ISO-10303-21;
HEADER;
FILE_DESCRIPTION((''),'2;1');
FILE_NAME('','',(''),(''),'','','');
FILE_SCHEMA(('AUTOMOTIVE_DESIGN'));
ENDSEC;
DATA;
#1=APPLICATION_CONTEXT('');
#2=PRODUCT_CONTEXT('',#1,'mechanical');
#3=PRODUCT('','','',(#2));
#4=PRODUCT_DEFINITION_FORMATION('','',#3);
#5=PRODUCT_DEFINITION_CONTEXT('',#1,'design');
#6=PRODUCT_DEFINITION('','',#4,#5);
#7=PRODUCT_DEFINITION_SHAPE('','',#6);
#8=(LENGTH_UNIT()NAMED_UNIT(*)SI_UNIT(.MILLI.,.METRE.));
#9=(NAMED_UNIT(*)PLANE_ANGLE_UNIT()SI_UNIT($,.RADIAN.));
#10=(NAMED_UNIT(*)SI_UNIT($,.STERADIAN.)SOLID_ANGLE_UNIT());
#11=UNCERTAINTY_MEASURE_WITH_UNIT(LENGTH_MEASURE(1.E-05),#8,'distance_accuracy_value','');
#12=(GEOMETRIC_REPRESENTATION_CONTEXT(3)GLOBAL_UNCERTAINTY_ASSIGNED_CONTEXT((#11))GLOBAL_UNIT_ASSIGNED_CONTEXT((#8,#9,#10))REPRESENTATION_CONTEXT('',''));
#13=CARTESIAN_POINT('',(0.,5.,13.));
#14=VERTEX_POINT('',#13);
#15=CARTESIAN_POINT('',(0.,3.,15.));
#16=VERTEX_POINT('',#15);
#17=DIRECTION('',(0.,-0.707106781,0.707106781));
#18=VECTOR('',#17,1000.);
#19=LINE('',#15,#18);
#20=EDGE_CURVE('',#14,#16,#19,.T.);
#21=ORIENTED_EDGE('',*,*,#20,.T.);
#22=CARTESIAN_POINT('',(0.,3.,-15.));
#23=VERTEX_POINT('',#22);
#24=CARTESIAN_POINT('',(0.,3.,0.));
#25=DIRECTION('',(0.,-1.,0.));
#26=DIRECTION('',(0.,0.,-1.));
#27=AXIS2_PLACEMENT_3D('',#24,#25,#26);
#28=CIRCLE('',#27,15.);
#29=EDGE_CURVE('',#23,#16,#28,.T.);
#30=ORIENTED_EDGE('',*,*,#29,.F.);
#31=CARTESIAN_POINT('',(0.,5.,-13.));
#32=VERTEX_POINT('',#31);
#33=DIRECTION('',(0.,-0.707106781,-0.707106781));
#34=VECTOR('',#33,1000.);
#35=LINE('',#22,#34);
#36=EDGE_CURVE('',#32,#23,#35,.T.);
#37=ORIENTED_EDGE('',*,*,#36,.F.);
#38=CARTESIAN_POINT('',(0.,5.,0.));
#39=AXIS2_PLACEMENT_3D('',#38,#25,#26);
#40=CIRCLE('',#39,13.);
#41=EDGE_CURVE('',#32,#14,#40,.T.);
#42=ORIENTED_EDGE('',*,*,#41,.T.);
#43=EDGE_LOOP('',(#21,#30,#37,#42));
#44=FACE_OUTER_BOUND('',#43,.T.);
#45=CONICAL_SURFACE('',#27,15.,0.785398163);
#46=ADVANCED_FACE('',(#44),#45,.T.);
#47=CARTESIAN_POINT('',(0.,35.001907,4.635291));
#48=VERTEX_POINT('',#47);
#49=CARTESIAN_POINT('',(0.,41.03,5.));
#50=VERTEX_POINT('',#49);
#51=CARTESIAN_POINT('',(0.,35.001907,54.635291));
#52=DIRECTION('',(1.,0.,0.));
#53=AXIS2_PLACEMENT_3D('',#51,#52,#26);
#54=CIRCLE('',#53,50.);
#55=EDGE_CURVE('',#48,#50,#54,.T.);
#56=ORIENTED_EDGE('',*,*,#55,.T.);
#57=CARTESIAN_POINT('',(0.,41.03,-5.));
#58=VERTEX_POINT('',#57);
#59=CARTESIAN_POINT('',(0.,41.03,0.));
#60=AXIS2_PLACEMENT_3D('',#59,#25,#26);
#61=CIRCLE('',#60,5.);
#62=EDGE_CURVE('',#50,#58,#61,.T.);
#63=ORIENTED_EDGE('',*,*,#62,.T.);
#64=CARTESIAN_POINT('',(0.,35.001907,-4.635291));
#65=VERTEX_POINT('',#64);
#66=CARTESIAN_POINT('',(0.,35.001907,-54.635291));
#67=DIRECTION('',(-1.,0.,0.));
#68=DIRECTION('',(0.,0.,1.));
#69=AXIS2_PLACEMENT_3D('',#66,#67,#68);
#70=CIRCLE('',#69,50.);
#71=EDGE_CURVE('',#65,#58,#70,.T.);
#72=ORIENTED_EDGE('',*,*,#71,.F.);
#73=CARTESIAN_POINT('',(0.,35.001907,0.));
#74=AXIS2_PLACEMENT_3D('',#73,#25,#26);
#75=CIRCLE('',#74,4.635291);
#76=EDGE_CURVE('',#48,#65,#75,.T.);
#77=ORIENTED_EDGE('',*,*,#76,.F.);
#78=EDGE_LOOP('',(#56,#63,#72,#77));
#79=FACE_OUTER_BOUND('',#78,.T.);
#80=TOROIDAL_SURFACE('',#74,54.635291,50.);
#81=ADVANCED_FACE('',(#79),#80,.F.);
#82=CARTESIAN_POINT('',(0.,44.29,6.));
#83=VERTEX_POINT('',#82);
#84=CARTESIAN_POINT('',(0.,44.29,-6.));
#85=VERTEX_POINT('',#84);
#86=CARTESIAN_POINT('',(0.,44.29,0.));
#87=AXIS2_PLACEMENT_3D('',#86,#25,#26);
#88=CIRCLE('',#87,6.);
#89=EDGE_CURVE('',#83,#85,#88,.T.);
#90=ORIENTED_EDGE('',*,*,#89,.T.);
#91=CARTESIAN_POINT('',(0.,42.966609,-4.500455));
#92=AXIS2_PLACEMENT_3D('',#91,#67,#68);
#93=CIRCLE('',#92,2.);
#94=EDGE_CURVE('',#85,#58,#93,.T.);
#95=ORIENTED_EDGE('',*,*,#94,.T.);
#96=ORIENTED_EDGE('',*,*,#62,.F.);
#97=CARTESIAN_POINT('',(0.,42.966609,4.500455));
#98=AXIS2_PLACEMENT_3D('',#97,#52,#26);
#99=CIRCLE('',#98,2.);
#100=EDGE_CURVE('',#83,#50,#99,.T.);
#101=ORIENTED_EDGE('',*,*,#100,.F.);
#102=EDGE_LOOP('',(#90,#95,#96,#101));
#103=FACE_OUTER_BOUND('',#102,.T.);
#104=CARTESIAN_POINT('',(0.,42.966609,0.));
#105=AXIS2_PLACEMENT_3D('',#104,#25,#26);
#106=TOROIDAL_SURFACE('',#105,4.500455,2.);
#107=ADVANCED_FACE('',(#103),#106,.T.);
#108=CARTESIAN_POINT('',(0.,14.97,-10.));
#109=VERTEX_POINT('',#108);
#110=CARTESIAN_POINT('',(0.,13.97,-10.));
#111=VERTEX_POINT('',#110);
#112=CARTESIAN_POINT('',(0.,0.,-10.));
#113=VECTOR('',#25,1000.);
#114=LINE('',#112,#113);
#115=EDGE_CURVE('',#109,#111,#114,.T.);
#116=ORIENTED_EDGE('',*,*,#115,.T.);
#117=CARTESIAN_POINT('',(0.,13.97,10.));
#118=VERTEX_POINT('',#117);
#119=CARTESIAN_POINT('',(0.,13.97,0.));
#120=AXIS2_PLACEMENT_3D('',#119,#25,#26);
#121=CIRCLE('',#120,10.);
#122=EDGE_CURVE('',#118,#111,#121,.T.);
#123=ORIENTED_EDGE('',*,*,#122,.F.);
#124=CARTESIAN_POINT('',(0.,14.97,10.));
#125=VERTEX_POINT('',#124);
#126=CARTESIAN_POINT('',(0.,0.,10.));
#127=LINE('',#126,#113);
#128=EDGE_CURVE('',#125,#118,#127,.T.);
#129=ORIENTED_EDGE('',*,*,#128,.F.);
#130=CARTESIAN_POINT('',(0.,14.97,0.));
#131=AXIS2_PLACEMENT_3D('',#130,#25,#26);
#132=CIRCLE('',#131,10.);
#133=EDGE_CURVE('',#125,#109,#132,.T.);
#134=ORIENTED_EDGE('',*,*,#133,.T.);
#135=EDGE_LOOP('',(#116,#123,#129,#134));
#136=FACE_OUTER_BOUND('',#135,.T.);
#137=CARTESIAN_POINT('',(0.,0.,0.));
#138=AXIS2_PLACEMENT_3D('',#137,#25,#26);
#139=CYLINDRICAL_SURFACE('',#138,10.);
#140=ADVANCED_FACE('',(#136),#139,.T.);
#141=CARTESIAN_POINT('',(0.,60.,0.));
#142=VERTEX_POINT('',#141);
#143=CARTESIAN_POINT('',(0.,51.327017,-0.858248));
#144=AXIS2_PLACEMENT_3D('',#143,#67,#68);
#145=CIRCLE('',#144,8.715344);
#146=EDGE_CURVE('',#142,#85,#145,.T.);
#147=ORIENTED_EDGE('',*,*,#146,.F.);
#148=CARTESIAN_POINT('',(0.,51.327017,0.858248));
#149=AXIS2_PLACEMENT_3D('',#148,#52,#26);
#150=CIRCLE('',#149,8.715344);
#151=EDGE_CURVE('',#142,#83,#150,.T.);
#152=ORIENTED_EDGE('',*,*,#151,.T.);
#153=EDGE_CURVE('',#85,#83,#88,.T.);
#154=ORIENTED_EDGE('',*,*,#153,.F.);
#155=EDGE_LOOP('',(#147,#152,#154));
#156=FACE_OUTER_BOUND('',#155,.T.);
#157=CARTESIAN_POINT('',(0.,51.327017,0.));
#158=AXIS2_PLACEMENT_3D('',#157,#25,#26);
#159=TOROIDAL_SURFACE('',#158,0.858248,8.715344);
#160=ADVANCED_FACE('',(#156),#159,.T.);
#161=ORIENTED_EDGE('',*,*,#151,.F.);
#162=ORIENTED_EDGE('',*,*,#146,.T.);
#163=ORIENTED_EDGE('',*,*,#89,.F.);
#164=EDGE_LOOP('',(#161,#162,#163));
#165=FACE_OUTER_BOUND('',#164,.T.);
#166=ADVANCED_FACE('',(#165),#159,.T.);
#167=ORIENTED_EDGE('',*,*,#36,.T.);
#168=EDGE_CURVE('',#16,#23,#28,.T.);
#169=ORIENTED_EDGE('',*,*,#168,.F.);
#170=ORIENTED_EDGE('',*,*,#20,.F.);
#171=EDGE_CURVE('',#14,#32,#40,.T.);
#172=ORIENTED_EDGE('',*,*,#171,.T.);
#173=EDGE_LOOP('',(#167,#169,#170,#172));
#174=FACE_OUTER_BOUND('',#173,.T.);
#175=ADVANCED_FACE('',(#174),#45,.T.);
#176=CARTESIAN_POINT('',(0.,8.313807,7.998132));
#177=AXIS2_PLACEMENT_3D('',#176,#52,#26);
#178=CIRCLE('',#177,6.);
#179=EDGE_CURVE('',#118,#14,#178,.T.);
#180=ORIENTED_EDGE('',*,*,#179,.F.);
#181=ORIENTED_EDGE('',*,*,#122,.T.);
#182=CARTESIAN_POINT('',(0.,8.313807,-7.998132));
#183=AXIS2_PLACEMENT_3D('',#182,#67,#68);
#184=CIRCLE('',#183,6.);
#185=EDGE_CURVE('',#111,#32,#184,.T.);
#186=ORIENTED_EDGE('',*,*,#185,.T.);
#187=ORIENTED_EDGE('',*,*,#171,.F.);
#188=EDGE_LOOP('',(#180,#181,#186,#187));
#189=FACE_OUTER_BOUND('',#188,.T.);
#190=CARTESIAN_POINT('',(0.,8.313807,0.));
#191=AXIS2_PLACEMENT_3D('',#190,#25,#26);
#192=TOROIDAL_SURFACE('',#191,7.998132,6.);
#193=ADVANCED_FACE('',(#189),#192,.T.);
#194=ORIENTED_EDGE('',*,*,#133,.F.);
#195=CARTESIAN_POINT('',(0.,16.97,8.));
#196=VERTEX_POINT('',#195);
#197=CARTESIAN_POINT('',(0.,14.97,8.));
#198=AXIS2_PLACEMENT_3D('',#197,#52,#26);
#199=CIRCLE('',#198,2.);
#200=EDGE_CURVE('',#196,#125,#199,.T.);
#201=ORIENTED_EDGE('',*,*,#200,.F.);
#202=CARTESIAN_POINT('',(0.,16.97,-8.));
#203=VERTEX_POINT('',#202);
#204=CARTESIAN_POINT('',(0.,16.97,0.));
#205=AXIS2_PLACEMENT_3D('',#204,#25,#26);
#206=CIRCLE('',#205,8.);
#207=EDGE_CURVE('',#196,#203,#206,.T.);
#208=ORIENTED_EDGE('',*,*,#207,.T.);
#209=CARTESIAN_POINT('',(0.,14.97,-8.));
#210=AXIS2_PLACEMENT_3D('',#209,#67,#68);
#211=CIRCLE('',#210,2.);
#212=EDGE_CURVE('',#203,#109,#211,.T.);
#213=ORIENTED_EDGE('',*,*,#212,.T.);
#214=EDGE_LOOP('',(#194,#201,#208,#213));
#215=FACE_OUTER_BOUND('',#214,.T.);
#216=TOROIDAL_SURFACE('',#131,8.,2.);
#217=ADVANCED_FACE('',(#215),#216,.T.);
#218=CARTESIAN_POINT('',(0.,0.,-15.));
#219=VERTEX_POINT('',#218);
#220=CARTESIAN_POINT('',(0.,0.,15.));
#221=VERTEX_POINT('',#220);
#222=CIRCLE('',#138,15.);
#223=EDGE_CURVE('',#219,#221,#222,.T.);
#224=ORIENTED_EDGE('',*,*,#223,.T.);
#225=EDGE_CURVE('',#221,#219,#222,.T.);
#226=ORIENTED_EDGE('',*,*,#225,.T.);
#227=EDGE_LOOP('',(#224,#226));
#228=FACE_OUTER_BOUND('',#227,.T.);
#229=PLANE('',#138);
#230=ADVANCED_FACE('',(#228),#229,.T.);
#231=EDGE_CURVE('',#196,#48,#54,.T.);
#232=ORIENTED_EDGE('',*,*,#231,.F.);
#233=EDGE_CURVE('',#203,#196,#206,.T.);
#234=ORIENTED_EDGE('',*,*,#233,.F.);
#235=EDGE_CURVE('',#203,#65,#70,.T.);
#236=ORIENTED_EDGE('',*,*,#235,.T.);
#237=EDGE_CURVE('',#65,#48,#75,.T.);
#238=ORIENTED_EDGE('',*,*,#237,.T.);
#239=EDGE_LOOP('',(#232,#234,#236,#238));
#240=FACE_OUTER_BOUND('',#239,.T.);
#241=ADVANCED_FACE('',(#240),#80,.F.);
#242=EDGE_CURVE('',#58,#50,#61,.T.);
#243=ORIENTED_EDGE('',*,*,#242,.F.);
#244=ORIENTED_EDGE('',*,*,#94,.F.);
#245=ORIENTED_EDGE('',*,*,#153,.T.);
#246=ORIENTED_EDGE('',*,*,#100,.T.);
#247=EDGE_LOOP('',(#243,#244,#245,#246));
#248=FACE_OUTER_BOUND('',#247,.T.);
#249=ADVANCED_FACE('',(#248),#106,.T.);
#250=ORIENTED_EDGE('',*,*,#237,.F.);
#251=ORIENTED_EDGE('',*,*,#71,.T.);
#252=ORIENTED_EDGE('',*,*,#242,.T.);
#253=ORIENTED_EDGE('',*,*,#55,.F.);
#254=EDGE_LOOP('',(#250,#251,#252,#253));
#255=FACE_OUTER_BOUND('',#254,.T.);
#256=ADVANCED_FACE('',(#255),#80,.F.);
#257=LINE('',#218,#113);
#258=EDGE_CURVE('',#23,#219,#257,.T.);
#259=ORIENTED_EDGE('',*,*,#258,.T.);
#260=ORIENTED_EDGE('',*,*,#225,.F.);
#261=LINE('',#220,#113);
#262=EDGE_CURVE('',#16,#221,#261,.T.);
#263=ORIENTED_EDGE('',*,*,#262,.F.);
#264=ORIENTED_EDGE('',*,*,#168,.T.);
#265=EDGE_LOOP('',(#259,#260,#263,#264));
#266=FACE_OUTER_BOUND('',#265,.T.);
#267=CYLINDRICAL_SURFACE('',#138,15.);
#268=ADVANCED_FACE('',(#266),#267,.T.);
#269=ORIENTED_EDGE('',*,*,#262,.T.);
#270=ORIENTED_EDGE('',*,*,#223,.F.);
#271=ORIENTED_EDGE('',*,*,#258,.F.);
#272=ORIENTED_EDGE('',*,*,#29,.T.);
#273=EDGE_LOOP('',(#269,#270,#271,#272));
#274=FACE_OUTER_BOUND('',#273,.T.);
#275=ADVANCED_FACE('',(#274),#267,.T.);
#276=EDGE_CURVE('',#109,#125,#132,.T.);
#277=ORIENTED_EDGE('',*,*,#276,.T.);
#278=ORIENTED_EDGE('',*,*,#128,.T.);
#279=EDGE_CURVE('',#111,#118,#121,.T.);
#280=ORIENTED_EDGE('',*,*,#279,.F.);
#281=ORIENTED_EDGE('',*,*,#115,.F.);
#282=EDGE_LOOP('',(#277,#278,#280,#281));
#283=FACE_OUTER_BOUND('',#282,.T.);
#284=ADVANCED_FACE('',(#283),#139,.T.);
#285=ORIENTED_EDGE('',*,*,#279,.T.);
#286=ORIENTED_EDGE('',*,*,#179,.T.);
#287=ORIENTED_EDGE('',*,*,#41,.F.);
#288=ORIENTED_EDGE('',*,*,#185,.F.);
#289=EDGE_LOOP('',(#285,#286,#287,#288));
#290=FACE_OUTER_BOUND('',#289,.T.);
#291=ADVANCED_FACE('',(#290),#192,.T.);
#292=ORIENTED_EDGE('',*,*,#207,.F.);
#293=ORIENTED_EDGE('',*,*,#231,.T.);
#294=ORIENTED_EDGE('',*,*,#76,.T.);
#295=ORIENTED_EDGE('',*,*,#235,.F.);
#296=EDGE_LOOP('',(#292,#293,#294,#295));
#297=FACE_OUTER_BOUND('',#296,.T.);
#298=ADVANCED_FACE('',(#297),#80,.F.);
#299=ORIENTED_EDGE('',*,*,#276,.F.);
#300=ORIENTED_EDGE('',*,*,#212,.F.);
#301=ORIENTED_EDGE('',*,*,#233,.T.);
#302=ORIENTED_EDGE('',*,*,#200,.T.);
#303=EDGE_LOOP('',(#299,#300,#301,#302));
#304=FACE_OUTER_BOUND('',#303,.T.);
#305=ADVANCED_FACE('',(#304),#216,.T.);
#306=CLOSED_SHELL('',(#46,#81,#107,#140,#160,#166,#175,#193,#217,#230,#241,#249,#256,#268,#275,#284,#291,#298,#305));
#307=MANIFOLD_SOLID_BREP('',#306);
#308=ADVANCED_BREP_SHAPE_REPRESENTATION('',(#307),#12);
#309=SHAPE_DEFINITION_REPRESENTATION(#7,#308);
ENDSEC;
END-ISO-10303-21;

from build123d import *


with BuildPart() as part:
    # Pawn Profile Sketch → Pawn Body Revolve (revolve)
    with BuildSketch(Plane.XY, mode=Mode.PRIVATE) as pawn_body_revolve_sk:
        with BuildLine():
            Line((0, 0), (15, 0))
            Line((15, 0), (15, 3))
            Line((15, 3), (13, 5))
            ThreePointArc((13, 5), (13.688325627, 10.216881481), (10, 13.97))
            Line((10, 13.97), (10, 14.97))
            ThreePointArc((10, 14.97), (9.414213562, 16.384213562), (8, 16.97))
            ThreePointArc((8, 16.97), (5.019495729, 28.81539847), (5, 41.03))
            ThreePointArc((5, 41.03), (6.412519214, 42.380086131), (6, 44.29))
            ThreePointArc((6, 44.29), (9, 54.436534055), (0, 60))
            Line((0, 60), (0, 0))
        make_face()
    revolve(pawn_body_revolve_sk.sketch.rotate(Axis((0, 0, 0), (0, 1, 0)), 90), axis=Axis((0, 0, 0), (0, 1, 0)))


solid = part.part
